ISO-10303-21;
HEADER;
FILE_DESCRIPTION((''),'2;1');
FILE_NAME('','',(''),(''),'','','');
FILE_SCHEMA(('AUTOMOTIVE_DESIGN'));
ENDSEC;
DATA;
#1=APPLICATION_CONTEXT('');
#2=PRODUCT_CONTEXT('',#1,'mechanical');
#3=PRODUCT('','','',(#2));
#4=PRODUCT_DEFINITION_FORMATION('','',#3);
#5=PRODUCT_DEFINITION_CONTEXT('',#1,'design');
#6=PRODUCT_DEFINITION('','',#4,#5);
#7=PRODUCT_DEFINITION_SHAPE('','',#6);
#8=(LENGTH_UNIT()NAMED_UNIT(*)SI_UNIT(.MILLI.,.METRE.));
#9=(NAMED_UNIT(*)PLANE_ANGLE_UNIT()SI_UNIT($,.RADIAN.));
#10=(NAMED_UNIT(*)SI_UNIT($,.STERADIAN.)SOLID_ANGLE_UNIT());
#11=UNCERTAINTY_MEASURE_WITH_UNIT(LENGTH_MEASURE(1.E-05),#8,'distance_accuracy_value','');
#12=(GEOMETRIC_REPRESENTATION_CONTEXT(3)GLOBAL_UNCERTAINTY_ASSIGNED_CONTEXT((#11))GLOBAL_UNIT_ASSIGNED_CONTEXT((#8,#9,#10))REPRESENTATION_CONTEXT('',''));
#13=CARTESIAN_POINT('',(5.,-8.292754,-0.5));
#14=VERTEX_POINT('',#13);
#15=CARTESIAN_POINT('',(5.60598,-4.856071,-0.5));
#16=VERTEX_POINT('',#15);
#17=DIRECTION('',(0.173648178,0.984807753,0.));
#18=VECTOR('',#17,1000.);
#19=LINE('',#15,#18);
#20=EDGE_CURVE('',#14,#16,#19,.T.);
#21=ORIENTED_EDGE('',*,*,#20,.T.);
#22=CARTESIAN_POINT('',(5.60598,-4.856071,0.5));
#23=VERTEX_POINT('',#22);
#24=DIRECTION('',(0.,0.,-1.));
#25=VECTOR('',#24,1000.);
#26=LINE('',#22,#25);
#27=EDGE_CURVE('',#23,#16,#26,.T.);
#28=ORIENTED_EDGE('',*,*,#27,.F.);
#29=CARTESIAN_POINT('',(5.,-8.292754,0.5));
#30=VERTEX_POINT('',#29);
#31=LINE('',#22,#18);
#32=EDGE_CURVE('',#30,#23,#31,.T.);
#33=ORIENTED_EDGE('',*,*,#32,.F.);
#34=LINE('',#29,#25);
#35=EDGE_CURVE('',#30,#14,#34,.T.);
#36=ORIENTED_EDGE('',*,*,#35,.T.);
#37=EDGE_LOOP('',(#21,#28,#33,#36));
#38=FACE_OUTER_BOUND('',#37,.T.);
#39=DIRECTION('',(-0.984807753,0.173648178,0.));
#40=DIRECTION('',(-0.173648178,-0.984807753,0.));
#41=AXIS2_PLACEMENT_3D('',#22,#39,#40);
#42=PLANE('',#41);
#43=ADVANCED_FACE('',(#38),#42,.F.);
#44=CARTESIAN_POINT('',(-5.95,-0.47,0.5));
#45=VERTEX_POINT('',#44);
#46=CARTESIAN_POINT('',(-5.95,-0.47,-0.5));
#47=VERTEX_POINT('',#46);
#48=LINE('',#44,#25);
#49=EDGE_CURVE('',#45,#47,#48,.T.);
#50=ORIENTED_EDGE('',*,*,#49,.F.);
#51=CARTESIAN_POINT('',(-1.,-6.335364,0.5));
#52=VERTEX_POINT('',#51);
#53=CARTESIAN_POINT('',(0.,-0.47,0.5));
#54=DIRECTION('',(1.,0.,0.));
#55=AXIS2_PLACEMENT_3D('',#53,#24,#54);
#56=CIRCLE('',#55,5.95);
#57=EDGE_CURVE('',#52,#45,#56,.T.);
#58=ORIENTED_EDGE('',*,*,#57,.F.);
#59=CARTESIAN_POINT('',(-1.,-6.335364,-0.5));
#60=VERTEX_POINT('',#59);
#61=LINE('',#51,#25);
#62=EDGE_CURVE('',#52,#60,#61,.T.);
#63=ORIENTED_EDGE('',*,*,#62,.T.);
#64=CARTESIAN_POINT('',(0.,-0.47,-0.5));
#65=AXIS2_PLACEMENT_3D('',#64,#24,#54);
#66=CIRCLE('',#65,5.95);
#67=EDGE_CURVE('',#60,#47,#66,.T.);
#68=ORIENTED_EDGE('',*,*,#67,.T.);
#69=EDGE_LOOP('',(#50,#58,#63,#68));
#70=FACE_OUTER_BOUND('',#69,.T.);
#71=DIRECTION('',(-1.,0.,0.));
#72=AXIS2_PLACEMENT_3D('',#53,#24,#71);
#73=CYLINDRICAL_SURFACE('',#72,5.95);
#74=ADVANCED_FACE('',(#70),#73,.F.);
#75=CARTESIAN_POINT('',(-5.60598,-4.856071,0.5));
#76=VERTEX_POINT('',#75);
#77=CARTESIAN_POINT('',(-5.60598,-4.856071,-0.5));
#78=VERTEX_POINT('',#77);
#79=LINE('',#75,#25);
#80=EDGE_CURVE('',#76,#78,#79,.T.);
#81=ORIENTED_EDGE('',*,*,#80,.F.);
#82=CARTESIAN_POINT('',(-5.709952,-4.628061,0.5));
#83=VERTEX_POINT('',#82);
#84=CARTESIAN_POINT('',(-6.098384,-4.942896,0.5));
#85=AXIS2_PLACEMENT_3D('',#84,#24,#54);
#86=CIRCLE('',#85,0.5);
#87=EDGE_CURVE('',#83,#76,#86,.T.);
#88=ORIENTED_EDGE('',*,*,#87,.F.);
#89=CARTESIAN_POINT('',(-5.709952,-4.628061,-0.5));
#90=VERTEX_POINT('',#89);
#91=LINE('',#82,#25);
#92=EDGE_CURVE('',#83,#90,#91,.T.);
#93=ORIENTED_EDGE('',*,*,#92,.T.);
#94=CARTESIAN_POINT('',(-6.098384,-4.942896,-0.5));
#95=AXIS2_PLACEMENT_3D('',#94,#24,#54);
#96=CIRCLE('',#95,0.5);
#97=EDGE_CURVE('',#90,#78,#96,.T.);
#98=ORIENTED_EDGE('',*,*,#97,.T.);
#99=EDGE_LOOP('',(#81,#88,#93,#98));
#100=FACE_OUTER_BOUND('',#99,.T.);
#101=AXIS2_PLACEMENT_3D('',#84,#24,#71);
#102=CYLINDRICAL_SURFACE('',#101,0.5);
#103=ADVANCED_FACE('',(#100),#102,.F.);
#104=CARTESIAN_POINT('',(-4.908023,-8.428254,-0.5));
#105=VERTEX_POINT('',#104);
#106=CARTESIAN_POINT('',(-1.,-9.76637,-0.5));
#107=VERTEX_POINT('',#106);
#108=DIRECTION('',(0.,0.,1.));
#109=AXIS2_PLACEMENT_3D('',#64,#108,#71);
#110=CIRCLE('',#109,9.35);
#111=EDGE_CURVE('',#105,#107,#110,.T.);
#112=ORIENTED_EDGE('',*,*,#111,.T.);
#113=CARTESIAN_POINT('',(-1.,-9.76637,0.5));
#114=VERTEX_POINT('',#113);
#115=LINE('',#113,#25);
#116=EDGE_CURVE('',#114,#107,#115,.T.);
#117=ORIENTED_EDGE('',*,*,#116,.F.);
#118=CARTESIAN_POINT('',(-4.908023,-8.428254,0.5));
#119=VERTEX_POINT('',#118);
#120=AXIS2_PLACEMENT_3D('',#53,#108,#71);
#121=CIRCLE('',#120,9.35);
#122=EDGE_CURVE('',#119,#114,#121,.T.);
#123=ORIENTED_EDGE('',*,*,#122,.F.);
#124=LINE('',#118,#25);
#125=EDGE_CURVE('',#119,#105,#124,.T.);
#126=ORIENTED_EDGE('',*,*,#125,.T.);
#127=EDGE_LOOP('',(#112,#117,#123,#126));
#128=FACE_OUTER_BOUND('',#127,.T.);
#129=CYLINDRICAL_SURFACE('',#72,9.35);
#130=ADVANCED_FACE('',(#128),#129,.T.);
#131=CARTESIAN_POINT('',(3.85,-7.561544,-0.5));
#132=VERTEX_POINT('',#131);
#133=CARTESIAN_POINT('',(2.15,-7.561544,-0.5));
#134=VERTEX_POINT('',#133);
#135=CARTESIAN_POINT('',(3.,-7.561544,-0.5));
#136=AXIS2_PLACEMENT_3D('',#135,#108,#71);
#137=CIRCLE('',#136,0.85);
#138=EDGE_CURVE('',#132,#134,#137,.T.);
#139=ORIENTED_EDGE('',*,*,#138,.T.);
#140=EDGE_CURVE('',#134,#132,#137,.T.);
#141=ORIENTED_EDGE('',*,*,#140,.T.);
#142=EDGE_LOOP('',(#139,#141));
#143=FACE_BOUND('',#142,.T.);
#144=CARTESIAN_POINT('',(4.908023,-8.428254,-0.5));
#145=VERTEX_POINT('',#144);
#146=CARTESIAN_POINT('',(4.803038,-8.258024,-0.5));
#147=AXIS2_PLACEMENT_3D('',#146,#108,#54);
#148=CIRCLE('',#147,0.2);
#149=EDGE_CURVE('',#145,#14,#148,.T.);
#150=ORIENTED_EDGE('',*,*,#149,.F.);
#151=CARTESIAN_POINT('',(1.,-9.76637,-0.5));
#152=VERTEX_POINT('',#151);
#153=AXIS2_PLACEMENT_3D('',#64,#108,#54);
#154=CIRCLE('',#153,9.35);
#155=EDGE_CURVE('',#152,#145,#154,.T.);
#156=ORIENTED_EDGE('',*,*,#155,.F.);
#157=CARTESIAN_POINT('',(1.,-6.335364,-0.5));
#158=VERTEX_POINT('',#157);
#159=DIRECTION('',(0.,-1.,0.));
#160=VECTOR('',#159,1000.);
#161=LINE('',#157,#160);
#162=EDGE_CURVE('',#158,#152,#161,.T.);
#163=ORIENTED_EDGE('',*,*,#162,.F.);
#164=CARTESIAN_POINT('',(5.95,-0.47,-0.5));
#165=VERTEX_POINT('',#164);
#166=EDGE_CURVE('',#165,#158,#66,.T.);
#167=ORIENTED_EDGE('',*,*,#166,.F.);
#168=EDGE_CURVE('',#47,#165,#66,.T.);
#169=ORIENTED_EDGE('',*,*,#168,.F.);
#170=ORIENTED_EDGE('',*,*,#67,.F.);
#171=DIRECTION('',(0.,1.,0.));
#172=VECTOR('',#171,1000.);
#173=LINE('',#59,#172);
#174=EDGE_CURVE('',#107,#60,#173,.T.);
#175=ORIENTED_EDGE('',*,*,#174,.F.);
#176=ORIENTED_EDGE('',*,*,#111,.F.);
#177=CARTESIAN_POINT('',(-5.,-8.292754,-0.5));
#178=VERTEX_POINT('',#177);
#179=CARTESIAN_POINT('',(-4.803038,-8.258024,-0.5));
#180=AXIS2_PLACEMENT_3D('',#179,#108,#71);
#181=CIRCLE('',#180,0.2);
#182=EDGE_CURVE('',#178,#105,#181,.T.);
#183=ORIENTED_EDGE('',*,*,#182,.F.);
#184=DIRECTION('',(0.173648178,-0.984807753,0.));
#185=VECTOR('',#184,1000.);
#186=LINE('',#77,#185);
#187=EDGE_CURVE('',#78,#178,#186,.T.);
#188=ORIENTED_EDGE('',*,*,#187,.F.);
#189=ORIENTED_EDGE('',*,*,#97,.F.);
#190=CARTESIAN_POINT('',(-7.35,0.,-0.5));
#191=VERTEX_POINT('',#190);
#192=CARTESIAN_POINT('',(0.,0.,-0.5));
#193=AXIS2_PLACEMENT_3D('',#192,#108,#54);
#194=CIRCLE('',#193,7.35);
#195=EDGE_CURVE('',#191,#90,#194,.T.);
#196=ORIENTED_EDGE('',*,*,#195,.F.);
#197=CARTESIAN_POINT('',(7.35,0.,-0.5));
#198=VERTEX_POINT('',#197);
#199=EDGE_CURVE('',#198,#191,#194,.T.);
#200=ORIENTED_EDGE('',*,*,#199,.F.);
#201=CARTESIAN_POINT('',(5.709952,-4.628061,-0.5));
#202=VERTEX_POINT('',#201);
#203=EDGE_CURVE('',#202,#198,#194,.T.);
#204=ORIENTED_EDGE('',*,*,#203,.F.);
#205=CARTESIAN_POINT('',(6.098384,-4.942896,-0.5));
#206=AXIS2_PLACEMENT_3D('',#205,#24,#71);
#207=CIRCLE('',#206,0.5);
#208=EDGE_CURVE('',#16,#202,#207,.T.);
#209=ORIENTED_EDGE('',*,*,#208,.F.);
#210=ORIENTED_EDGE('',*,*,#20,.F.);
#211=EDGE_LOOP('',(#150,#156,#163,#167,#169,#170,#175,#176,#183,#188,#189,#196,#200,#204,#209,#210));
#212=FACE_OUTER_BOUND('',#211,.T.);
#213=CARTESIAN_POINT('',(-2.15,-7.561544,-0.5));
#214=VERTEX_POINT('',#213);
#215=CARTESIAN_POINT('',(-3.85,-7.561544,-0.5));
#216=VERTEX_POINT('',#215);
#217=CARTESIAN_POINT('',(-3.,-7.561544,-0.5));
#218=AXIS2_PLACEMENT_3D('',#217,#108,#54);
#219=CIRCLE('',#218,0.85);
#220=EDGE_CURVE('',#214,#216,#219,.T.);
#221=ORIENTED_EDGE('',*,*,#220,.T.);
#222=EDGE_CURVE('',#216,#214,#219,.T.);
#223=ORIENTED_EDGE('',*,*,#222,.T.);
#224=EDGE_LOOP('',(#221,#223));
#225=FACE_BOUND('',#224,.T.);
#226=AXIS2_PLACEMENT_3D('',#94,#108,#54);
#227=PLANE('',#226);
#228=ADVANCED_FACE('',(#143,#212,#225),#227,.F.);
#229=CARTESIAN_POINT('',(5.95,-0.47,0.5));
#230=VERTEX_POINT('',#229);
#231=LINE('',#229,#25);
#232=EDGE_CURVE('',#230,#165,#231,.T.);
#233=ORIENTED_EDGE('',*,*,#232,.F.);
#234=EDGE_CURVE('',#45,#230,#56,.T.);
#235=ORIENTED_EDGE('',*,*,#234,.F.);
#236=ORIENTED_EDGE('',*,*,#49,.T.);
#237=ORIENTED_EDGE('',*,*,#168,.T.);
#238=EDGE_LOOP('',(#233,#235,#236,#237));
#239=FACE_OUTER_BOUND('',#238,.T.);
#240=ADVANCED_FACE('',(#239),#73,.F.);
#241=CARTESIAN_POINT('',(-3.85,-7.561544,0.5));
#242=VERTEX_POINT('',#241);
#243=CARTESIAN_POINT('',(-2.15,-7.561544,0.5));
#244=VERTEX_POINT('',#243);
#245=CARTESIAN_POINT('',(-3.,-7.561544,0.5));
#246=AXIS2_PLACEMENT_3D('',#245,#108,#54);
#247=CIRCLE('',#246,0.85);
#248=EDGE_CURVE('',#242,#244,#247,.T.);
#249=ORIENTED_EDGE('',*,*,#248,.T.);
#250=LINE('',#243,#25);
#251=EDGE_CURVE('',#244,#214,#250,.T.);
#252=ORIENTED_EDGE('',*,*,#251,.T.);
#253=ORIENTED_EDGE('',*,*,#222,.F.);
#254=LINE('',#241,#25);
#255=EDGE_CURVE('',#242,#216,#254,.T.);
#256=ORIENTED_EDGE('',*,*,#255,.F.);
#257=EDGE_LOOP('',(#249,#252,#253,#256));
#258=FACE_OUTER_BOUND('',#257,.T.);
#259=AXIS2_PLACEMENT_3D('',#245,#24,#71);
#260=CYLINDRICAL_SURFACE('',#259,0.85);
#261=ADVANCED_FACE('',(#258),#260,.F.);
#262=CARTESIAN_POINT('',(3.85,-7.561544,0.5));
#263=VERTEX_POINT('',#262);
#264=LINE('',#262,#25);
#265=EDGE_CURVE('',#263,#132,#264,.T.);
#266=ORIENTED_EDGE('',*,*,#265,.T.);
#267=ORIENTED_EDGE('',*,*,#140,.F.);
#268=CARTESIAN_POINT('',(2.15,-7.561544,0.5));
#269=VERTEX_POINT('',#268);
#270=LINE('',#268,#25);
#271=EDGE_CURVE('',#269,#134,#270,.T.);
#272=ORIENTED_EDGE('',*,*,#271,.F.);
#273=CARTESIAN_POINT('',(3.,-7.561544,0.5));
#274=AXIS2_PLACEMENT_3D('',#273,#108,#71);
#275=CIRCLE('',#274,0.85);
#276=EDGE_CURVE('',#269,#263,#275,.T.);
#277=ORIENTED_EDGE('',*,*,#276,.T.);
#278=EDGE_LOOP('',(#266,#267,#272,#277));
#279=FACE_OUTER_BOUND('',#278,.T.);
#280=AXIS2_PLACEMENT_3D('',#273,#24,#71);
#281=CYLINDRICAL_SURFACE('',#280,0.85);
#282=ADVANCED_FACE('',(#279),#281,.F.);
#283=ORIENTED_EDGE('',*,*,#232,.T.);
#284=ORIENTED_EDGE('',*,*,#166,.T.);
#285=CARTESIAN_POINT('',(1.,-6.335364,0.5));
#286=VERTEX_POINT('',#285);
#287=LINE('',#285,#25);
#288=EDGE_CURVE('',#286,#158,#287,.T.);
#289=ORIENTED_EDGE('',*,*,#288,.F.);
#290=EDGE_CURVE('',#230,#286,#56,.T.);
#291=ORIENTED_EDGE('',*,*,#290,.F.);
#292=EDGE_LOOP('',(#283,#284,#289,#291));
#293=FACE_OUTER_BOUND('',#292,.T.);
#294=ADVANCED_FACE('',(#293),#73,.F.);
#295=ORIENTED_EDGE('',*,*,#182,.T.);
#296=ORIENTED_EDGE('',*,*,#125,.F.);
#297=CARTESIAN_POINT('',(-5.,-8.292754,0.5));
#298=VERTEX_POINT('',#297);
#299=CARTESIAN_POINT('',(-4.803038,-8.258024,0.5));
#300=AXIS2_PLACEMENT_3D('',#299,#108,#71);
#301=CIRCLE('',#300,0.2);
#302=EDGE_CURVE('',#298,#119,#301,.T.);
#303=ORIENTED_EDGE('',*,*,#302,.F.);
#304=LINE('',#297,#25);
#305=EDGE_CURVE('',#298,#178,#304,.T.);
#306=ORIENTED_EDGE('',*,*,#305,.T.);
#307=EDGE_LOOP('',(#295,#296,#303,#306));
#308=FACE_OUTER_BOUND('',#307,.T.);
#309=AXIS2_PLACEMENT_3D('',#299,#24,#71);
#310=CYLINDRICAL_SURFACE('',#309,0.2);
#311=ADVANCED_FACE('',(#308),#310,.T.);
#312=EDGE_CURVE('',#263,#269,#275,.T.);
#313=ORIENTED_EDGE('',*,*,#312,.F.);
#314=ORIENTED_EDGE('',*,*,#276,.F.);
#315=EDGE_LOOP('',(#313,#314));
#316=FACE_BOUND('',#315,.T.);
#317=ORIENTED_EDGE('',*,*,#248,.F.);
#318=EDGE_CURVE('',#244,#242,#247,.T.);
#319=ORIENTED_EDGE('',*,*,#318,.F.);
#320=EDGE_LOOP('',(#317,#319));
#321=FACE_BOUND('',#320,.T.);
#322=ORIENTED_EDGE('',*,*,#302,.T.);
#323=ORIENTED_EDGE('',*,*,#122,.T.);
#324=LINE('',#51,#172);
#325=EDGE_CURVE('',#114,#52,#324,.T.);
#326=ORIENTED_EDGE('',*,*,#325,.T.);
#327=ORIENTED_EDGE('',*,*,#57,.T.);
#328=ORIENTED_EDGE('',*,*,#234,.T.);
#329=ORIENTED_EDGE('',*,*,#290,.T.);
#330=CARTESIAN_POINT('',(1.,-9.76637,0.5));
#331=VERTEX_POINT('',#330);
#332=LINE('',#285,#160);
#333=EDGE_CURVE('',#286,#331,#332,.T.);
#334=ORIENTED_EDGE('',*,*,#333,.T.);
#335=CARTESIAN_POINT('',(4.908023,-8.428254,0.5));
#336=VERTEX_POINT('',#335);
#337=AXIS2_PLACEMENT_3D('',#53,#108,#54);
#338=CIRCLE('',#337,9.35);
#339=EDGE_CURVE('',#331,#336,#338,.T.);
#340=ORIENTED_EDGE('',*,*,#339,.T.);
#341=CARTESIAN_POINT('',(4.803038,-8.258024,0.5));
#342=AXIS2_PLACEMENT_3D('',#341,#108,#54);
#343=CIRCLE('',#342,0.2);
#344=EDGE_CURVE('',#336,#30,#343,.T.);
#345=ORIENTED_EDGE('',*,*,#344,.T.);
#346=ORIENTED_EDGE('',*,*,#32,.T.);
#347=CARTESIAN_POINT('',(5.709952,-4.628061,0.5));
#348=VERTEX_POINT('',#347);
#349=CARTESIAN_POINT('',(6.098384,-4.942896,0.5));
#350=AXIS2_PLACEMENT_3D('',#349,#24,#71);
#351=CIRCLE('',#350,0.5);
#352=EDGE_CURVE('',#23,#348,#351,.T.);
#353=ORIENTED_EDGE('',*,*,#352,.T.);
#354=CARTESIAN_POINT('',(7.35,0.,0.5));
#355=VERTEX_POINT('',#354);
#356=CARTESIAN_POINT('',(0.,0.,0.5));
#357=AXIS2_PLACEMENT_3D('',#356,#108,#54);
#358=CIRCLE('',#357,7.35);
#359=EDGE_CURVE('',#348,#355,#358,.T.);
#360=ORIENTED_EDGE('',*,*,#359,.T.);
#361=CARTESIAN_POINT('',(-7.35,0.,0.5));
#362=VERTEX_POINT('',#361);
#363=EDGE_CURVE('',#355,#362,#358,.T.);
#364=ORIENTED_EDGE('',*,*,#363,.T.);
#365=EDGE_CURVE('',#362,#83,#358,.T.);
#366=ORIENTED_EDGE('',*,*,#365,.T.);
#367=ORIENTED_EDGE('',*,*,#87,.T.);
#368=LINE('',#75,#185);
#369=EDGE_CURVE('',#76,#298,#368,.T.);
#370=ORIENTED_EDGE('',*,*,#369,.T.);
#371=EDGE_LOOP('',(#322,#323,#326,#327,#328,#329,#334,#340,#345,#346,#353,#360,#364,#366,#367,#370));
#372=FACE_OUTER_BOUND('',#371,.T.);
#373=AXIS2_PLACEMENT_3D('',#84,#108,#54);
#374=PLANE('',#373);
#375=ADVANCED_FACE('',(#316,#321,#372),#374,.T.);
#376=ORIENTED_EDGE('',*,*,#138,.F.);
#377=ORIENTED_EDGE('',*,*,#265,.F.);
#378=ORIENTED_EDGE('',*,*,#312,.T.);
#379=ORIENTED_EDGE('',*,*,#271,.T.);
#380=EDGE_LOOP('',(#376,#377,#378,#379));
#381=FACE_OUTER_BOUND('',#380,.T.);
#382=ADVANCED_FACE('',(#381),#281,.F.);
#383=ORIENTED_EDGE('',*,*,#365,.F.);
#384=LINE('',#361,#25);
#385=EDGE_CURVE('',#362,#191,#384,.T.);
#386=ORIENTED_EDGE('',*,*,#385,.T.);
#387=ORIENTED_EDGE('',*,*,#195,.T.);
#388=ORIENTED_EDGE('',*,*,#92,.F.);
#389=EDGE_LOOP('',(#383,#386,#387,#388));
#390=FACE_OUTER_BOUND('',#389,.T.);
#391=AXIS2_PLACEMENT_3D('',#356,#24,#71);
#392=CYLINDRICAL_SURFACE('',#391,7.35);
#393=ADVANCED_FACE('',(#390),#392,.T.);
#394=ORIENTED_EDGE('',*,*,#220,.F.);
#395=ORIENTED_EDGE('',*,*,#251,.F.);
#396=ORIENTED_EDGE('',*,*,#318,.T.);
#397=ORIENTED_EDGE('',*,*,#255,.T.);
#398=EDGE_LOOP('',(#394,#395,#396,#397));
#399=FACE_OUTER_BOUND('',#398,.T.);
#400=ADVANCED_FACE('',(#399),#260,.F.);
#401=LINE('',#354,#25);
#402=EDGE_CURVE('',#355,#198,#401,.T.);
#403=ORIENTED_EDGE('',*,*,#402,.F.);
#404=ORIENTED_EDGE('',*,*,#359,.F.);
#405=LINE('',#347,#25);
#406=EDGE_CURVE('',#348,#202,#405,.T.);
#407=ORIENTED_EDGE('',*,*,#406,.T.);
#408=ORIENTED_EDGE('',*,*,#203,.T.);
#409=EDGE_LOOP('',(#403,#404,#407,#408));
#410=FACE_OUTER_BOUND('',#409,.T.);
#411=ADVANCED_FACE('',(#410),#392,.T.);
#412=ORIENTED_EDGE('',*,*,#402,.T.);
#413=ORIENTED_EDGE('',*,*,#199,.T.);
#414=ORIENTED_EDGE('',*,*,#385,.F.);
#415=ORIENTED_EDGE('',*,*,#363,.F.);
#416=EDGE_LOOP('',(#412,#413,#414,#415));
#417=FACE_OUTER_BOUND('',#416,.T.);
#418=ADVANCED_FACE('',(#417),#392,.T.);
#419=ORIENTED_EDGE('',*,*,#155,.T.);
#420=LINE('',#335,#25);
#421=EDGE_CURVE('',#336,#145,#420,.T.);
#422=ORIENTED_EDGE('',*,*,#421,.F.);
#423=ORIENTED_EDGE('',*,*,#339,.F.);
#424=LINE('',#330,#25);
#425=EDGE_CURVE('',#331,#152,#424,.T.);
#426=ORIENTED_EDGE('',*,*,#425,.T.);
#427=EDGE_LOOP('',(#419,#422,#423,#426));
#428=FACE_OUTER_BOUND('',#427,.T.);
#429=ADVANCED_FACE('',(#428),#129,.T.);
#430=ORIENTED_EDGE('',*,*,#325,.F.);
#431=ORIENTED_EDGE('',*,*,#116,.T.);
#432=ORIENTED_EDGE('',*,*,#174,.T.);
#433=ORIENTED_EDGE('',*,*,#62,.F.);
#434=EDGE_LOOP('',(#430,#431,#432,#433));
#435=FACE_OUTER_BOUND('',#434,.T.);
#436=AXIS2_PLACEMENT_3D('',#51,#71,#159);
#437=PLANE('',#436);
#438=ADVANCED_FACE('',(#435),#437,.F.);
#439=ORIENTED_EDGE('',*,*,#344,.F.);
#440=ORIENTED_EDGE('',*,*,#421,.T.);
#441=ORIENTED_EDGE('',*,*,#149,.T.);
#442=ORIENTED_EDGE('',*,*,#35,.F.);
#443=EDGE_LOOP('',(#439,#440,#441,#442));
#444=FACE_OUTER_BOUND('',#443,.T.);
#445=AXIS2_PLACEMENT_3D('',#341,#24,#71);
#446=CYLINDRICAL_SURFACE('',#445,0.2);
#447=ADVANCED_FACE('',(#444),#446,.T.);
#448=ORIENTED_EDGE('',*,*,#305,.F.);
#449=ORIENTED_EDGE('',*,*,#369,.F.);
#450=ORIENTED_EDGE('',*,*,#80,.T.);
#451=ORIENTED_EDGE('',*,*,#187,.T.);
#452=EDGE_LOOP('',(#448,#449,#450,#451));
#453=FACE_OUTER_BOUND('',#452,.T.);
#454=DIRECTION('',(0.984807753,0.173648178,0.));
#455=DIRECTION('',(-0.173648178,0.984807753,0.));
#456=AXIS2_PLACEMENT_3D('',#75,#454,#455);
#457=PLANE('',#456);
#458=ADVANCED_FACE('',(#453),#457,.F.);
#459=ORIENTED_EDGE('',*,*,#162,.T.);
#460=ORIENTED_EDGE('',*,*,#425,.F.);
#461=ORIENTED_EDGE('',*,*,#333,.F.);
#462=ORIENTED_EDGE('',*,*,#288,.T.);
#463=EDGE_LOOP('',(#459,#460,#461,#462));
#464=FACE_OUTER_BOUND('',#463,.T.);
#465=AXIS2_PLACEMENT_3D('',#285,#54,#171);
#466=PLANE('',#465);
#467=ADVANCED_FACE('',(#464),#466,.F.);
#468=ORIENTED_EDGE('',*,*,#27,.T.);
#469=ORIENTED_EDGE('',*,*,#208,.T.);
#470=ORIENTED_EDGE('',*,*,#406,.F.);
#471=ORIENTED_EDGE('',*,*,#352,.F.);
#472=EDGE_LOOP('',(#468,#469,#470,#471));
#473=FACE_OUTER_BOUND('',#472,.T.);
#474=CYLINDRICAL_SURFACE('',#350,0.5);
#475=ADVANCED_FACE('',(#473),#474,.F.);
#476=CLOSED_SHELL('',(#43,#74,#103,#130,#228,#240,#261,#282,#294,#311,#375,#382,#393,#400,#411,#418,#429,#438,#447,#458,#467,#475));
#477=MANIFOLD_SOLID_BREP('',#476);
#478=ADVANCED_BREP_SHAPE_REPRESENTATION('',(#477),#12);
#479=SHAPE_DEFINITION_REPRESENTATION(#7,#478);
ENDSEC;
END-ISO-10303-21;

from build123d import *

# Parameters (mm, degrees)
BASE_EXTRUDE_DEPTH      = 0.5
BASE_EXTRUDE_DEPTH_BACK = 0.5
SKETCH1_R               = 0.85


with BuildPart() as part:
    # Sketch1 → Base-Extrude (new, two sides: drawn at the far end of the back side and taken through both)
    with BuildSketch(Plane.XY.offset(-BASE_EXTRUDE_DEPTH_BACK)):
        with BuildLine():
            Line((-1, -6.335364439), (-1, -9.766370259))
            ThreePointArc((-1, -9.766370259), (-3.028831825, -9.315828269), (-4.908022896, -8.428254284))
            ThreePointArc((-4.908022896, -8.428254284), (-4.968516352, -8.37034995), (-5, -8.292753881))
            Line((-5, -8.292753881), (-5.605979842, -4.856071421))
            ThreePointArc((-5.605979842, -4.856071421), (-5.643449504, -4.735447058), (-5.709951634, -4.628061401))
            ThreePointArc((-5.709951634, -4.628061401), (0, 7.35), (5.709951634, -4.628061401))
            ThreePointArc((5.709951634, -4.628061401), (5.643449504, -4.735447058), (5.605979842, -4.856071421))
            Line((5.605979842, -4.856071421), (5, -8.292753881))
            ThreePointArc((5, -8.292753881), (4.968516352, -8.37034995), (4.908022896, -8.428254284))
            ThreePointArc((4.908022896, -8.428254284), (3.028831825, -9.315828269), (1, -9.766370259))
            Line((1, -9.766370259), (1, -6.335364439))
            ThreePointArc((1, -6.335364439), (0, 5.48), (-1, -6.335364439))
        make_face()
        with Locations((-3, -7.561544261)):
            Circle(SKETCH1_R, mode=Mode.SUBTRACT)
        with Locations(Location((3, -7.561544261, 0), (0, 0, 180))):
            Circle(SKETCH1_R, mode=Mode.SUBTRACT)
    extrude(amount=BASE_EXTRUDE_DEPTH + BASE_EXTRUDE_DEPTH_BACK)


solid = part.part
